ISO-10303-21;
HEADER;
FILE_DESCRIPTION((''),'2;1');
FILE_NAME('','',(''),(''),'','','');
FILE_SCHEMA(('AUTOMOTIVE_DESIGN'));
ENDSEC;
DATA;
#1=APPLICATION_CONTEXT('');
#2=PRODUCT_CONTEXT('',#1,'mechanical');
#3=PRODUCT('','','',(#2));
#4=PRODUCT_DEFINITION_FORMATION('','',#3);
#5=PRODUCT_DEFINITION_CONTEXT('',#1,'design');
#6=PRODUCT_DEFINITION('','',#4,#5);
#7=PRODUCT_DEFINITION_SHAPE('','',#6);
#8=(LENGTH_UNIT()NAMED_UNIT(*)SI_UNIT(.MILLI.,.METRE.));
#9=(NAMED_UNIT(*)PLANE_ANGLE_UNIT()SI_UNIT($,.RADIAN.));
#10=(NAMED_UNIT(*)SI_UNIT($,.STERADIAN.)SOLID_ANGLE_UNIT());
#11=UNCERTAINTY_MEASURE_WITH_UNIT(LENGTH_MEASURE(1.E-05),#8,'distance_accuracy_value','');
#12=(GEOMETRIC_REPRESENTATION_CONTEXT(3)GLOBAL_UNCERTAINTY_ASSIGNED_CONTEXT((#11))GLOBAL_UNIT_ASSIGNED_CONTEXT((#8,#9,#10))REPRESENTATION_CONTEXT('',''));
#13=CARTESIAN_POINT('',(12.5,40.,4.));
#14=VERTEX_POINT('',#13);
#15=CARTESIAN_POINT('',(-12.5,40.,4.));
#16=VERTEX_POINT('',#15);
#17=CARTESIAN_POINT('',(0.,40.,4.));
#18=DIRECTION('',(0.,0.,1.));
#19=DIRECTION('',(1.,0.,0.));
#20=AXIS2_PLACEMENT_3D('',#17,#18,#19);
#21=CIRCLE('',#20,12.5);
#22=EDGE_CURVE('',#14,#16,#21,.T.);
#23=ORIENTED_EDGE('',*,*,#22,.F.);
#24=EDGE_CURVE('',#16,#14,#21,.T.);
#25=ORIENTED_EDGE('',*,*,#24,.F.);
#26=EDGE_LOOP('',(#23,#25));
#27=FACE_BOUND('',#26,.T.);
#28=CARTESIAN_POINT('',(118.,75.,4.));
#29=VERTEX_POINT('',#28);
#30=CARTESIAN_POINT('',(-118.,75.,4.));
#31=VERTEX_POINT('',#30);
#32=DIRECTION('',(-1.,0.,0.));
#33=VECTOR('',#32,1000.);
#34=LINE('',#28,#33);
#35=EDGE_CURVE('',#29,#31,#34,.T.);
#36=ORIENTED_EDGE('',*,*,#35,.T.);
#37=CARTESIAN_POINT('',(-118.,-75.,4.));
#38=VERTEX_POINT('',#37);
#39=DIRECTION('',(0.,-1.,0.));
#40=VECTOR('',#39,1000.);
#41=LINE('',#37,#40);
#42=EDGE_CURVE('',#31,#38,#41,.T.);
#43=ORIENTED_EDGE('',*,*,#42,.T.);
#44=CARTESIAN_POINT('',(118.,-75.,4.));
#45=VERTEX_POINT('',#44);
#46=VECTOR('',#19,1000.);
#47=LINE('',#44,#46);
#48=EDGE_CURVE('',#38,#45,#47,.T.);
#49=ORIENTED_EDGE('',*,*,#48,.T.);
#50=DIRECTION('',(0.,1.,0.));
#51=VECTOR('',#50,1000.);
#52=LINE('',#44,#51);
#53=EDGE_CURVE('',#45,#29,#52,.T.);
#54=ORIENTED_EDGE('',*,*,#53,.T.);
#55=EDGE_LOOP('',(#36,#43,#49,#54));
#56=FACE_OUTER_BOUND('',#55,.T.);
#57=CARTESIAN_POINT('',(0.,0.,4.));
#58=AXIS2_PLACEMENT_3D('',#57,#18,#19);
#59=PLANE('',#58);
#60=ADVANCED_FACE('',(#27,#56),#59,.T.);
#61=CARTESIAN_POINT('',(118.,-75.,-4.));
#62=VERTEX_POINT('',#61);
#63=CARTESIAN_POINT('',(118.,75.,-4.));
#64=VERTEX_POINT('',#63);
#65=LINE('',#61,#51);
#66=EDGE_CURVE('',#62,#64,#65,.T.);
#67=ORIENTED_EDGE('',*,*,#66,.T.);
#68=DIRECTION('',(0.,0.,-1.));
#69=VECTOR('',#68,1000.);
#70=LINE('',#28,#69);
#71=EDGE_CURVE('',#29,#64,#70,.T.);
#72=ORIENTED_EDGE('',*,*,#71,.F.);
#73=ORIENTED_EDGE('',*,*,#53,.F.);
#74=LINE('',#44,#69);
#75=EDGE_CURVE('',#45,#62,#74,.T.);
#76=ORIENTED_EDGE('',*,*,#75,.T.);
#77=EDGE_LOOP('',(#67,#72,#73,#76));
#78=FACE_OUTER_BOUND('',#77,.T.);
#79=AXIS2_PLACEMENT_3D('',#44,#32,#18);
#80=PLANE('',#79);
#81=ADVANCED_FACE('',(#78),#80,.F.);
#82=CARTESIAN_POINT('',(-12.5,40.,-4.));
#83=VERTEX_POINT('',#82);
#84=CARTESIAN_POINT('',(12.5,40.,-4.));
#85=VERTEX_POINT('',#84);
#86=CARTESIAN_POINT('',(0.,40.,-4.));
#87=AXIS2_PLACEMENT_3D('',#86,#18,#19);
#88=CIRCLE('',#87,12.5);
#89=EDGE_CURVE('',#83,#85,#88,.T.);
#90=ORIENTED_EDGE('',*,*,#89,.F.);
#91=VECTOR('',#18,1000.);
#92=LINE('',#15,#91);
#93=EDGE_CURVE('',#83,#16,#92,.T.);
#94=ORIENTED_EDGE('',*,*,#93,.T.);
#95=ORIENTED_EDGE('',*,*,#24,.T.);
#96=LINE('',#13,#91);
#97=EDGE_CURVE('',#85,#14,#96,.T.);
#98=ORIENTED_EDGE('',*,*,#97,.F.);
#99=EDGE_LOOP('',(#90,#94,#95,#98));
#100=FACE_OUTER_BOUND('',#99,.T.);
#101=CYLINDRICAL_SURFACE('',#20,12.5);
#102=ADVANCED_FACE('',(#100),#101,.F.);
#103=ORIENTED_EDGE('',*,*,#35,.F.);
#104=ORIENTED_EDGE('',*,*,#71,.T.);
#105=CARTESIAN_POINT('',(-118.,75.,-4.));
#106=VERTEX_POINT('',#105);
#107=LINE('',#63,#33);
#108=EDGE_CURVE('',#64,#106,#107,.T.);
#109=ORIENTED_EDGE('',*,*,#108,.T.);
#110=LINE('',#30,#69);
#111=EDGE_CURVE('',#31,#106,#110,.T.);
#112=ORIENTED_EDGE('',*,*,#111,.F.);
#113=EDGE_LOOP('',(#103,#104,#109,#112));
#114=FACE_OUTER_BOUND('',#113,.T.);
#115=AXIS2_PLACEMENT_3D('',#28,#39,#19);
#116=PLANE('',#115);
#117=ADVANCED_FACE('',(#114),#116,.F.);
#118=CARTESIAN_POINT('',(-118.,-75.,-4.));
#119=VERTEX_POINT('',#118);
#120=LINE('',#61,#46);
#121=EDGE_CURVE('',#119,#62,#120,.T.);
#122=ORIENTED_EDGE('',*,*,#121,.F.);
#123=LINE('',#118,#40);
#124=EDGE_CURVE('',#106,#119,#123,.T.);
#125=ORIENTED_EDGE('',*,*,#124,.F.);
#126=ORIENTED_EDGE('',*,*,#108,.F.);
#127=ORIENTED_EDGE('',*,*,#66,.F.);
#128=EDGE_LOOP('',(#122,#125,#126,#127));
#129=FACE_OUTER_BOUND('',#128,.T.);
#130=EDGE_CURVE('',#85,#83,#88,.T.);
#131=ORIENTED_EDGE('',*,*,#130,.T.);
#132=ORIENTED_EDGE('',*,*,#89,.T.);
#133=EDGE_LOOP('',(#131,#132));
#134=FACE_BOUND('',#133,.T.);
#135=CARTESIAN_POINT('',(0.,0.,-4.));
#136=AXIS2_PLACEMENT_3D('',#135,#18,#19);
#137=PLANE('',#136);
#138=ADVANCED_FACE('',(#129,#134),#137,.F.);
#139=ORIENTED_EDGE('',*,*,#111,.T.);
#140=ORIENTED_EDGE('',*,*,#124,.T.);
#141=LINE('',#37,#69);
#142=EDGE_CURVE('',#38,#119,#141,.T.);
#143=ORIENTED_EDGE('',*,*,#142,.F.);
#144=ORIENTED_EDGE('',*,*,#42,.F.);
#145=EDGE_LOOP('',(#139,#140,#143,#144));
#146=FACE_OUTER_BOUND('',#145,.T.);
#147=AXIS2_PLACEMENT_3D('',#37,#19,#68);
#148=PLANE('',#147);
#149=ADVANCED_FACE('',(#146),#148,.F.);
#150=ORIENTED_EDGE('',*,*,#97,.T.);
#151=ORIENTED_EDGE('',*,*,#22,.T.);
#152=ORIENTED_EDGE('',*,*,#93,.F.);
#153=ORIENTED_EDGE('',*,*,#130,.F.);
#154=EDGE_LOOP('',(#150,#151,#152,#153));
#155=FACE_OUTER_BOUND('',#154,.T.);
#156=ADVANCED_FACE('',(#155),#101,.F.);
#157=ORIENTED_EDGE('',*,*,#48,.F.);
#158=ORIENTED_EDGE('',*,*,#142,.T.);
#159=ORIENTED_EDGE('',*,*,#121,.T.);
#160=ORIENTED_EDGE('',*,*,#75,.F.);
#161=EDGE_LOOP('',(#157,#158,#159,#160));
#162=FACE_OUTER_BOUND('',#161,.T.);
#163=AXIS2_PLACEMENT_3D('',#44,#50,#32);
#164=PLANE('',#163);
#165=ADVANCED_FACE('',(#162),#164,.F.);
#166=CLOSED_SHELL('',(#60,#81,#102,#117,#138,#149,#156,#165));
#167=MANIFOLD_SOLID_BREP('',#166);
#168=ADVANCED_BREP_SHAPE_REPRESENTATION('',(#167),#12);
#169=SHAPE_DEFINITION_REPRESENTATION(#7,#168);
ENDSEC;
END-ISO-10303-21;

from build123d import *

# Parameters (mm, degrees)
SKETCH1_W                  = 236
SKETCH1_H                  = 150
BOSS_EXTRUDE1_DEPTH        = 4
F_25_0_25_DIAMETER_HOLE1_D = 25


with BuildPart() as part:
    # Sketch1 → Boss-Extrude1 (new, symmetric)
    with BuildSketch(Plane.XY):
        Rectangle(SKETCH1_W, SKETCH1_H)
    extrude(amount=BOSS_EXTRUDE1_DEPTH, both=True)

    # Ø25.0 (25) Diameter Hole1 (through all)
    with Locations(Plane.XY.offset(4)):
        with Locations((0, 40)):
            Hole(F_25_0_25_DIAMETER_HOLE1_D / 2)


solid = part.part
